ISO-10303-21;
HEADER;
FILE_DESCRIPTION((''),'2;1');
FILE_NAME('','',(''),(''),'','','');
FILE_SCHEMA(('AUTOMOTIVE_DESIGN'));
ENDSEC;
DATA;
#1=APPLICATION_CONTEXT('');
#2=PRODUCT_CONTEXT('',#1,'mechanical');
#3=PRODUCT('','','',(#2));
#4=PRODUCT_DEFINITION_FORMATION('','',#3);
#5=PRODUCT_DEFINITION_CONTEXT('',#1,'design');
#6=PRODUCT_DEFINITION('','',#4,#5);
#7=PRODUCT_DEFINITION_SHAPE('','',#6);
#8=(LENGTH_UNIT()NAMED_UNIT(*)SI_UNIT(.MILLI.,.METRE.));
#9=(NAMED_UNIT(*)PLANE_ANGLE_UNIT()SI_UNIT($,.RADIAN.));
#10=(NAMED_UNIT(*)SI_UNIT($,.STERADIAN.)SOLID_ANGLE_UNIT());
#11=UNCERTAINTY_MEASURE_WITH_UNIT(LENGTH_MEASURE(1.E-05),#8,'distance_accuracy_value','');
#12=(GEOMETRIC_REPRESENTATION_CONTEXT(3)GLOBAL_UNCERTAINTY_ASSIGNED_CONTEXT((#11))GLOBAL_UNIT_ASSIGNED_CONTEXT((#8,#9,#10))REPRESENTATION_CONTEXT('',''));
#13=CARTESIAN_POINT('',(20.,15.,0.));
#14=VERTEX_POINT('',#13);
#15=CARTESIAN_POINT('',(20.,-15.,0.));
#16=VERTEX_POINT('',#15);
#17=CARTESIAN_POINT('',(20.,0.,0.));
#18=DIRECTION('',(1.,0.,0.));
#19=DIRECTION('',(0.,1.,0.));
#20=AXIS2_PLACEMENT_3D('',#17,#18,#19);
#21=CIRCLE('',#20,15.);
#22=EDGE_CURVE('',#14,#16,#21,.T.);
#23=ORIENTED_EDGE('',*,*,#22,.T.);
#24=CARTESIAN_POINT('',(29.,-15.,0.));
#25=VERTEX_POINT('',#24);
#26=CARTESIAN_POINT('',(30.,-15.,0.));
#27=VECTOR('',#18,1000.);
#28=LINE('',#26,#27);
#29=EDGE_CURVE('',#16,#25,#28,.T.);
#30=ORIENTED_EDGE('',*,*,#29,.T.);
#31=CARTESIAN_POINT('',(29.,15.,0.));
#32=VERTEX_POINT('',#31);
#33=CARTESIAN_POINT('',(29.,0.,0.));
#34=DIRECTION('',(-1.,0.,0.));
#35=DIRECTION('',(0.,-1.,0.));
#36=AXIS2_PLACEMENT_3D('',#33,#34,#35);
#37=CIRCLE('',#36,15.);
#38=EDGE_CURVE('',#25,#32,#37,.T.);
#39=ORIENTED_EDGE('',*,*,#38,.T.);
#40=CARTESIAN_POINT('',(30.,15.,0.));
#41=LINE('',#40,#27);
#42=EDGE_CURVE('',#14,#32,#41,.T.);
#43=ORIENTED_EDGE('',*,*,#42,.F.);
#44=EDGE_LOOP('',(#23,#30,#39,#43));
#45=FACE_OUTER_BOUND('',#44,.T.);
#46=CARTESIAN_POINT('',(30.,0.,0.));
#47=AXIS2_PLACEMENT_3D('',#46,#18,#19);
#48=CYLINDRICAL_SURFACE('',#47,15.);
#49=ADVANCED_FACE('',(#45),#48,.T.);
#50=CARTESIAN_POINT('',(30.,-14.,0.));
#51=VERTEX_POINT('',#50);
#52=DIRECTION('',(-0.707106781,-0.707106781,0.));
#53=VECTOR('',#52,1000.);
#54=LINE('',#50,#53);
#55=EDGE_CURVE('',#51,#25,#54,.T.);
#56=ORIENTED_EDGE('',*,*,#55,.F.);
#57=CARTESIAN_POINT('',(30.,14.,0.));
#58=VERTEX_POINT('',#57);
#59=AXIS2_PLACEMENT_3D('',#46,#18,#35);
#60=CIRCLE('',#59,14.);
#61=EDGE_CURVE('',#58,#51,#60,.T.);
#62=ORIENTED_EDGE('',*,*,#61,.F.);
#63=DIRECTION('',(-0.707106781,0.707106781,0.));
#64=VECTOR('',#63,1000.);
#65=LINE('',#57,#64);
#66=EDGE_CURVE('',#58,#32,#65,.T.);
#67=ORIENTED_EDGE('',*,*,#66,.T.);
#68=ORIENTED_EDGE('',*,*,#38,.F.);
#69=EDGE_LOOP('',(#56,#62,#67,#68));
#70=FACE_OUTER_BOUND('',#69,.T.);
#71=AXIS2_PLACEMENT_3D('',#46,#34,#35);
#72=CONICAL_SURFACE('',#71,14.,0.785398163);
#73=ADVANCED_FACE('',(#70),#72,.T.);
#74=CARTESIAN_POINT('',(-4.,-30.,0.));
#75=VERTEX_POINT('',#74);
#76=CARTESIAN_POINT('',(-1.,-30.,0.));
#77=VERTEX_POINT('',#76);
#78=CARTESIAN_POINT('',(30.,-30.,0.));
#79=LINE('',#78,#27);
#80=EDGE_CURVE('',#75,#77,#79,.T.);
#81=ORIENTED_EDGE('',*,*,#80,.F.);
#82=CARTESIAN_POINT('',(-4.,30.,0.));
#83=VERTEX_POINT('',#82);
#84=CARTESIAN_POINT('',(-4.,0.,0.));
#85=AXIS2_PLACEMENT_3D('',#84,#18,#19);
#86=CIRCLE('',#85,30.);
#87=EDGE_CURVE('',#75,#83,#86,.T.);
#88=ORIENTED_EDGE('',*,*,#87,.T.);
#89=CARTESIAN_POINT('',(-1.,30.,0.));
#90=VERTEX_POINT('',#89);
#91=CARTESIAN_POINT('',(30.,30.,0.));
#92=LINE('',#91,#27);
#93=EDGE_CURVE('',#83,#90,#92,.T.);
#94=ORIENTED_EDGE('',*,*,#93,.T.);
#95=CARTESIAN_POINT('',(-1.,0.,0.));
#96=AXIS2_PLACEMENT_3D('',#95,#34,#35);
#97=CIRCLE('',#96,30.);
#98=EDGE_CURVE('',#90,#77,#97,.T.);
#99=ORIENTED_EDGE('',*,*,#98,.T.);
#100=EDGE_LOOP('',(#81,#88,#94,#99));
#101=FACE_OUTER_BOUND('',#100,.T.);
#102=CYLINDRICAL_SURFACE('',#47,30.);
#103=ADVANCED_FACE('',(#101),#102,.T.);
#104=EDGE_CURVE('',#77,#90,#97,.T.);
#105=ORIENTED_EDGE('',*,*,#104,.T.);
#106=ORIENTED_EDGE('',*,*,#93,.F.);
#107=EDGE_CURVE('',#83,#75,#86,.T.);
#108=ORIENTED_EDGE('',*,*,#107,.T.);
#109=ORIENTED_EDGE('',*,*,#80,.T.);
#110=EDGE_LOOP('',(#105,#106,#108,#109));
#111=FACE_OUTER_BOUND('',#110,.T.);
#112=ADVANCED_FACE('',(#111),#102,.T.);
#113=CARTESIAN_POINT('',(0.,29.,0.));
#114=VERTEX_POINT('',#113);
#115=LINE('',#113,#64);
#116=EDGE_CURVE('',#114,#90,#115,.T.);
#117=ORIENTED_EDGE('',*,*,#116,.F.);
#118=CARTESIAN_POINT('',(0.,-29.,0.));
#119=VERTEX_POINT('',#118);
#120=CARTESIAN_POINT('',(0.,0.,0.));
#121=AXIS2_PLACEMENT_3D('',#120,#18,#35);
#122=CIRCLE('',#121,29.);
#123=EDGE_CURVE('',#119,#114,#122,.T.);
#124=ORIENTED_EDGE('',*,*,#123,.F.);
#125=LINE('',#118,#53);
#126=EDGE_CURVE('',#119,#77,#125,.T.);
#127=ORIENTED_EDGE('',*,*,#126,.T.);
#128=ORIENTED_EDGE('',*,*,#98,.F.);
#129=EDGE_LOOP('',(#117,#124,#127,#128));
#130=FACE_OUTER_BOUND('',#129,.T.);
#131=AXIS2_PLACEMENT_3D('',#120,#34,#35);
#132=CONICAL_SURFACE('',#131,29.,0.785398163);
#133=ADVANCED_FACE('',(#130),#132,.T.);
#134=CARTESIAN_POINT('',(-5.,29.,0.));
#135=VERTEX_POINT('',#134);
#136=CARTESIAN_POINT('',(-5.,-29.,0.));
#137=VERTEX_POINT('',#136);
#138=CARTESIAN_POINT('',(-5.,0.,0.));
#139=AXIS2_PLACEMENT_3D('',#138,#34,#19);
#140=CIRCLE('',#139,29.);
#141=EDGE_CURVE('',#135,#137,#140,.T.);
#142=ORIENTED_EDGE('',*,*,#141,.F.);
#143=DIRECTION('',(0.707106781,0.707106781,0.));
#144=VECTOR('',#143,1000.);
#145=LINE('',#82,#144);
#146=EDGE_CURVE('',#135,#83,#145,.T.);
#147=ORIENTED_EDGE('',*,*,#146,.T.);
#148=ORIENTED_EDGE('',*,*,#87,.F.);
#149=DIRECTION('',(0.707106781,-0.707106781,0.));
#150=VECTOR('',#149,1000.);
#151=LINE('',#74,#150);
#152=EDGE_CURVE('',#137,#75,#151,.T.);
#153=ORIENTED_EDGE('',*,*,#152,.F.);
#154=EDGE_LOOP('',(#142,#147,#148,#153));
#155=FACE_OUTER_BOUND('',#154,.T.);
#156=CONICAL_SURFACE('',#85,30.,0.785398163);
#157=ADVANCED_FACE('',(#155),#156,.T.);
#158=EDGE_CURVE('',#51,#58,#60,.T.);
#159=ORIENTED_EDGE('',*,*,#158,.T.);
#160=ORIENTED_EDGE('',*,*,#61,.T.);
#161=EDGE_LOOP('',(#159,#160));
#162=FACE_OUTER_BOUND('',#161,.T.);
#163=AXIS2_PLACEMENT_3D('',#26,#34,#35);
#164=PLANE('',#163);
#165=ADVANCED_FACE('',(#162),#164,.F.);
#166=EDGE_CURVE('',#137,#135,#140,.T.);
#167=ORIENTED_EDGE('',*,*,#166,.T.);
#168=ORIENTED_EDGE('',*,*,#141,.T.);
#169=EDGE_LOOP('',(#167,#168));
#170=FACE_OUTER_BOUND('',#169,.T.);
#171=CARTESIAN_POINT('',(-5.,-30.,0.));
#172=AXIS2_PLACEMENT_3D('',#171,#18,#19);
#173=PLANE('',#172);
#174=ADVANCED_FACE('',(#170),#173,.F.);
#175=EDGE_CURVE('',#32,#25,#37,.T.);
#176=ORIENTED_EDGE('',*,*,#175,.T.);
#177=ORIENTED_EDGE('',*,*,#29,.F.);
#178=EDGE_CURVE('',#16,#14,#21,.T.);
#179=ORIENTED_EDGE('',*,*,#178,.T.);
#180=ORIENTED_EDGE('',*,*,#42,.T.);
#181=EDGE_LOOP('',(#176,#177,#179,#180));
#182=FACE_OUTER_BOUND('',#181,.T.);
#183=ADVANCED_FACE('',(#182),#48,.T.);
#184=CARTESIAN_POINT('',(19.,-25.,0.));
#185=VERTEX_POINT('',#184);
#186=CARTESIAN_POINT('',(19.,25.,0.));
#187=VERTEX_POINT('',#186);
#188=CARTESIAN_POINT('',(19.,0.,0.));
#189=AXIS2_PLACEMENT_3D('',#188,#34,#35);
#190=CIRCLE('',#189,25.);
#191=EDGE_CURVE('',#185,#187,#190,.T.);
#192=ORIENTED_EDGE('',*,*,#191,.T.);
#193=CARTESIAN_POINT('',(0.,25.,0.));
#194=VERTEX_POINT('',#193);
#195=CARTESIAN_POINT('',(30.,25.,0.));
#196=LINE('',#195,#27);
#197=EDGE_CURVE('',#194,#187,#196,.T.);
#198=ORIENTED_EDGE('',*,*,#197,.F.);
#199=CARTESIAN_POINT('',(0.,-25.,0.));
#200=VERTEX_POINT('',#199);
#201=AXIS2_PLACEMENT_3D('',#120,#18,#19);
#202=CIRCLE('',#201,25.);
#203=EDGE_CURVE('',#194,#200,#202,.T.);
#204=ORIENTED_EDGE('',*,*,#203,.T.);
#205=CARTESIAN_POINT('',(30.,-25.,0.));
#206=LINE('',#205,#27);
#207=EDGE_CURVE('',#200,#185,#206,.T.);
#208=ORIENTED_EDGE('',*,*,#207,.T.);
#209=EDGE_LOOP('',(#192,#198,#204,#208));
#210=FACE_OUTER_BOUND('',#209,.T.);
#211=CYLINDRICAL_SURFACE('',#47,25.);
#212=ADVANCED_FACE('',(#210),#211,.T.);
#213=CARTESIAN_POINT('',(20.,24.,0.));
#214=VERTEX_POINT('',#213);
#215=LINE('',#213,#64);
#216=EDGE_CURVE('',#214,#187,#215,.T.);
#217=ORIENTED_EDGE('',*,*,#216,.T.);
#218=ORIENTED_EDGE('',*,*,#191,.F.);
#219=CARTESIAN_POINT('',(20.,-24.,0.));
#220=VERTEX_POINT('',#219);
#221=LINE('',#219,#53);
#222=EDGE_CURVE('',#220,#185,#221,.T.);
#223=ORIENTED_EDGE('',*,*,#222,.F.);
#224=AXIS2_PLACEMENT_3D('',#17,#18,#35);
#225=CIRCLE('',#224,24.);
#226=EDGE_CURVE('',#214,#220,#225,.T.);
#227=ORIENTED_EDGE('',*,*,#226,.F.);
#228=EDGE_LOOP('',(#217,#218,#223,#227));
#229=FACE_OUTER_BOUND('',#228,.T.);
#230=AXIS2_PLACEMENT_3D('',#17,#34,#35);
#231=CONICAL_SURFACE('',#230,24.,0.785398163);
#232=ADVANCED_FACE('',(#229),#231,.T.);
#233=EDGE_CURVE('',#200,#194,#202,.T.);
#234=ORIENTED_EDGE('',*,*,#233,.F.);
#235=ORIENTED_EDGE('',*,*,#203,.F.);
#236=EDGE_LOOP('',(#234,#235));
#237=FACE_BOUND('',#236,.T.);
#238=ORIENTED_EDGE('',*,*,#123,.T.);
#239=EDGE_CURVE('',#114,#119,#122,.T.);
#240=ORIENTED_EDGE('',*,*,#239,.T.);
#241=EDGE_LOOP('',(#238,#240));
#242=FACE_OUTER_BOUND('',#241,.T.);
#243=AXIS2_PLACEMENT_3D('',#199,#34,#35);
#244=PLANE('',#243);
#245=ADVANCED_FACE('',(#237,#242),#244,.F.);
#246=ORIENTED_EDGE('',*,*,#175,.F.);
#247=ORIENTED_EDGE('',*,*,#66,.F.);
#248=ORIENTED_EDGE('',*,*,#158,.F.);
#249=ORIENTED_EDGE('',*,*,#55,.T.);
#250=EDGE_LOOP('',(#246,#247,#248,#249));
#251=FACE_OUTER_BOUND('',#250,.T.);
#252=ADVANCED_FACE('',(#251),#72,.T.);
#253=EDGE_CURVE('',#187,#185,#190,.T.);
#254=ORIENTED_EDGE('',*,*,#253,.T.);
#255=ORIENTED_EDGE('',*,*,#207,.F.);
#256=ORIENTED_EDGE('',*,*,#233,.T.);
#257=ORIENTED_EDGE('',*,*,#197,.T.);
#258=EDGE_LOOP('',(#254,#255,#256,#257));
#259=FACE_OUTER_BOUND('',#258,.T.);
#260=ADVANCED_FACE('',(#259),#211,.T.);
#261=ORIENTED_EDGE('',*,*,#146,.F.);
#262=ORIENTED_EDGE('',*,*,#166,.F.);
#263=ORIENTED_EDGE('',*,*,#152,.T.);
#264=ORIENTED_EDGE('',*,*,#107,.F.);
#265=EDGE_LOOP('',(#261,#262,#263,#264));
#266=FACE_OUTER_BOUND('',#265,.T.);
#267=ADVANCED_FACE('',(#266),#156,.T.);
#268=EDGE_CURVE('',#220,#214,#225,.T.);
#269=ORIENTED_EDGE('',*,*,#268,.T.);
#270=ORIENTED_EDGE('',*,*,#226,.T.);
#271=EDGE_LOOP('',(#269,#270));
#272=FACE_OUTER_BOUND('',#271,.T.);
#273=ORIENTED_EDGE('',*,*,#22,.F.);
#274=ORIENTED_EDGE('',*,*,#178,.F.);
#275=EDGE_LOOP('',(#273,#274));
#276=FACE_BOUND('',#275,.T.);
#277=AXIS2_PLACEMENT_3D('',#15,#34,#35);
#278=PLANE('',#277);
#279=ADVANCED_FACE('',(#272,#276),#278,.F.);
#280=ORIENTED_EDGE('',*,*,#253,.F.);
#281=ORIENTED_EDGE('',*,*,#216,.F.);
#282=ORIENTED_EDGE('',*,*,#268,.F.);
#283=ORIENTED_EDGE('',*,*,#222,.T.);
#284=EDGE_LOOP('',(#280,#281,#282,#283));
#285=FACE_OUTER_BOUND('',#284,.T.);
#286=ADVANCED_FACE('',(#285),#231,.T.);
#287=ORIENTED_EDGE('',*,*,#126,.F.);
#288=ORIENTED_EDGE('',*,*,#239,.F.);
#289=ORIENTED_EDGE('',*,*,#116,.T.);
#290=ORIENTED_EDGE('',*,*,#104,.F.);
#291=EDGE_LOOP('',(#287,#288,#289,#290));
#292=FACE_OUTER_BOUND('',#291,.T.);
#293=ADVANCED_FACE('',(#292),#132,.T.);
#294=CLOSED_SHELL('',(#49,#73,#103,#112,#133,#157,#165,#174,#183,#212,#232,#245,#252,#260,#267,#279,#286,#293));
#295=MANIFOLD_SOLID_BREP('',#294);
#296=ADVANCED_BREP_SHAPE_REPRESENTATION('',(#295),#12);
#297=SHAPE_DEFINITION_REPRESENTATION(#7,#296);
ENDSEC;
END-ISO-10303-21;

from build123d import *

# Parameters (mm, degrees)
CHAMFER1_SIZE = 1


with BuildPart() as part:
    # Sketch1 → Revolve1 (revolve)
    with BuildSketch(Plane.XY, mode=Mode.PRIVATE) as revolve1_sk:
        Polygon((30, -15), (20, -15), (20, -25), (0, -25), (0, -30), (-5, -30), (-5, 0), (30, 0), align=None)
    revolve(revolve1_sk.sketch.rotate(Axis((30, 0, 0), (-1, 0, 0)), 180), axis=Axis((30, 0, 0), (-1, 0, 0)))

    # Chamfer1
    chamfer1_edges = [part.edges().sort_by_distance(p)[0] for p in [
        (30, -15, 0),
        (20, -25, 0),
        (0, -30, 0),
        (-5, -30, 0),
    ]]
    chamfer(chamfer1_edges, length=CHAMFER1_SIZE)


solid = part.part
